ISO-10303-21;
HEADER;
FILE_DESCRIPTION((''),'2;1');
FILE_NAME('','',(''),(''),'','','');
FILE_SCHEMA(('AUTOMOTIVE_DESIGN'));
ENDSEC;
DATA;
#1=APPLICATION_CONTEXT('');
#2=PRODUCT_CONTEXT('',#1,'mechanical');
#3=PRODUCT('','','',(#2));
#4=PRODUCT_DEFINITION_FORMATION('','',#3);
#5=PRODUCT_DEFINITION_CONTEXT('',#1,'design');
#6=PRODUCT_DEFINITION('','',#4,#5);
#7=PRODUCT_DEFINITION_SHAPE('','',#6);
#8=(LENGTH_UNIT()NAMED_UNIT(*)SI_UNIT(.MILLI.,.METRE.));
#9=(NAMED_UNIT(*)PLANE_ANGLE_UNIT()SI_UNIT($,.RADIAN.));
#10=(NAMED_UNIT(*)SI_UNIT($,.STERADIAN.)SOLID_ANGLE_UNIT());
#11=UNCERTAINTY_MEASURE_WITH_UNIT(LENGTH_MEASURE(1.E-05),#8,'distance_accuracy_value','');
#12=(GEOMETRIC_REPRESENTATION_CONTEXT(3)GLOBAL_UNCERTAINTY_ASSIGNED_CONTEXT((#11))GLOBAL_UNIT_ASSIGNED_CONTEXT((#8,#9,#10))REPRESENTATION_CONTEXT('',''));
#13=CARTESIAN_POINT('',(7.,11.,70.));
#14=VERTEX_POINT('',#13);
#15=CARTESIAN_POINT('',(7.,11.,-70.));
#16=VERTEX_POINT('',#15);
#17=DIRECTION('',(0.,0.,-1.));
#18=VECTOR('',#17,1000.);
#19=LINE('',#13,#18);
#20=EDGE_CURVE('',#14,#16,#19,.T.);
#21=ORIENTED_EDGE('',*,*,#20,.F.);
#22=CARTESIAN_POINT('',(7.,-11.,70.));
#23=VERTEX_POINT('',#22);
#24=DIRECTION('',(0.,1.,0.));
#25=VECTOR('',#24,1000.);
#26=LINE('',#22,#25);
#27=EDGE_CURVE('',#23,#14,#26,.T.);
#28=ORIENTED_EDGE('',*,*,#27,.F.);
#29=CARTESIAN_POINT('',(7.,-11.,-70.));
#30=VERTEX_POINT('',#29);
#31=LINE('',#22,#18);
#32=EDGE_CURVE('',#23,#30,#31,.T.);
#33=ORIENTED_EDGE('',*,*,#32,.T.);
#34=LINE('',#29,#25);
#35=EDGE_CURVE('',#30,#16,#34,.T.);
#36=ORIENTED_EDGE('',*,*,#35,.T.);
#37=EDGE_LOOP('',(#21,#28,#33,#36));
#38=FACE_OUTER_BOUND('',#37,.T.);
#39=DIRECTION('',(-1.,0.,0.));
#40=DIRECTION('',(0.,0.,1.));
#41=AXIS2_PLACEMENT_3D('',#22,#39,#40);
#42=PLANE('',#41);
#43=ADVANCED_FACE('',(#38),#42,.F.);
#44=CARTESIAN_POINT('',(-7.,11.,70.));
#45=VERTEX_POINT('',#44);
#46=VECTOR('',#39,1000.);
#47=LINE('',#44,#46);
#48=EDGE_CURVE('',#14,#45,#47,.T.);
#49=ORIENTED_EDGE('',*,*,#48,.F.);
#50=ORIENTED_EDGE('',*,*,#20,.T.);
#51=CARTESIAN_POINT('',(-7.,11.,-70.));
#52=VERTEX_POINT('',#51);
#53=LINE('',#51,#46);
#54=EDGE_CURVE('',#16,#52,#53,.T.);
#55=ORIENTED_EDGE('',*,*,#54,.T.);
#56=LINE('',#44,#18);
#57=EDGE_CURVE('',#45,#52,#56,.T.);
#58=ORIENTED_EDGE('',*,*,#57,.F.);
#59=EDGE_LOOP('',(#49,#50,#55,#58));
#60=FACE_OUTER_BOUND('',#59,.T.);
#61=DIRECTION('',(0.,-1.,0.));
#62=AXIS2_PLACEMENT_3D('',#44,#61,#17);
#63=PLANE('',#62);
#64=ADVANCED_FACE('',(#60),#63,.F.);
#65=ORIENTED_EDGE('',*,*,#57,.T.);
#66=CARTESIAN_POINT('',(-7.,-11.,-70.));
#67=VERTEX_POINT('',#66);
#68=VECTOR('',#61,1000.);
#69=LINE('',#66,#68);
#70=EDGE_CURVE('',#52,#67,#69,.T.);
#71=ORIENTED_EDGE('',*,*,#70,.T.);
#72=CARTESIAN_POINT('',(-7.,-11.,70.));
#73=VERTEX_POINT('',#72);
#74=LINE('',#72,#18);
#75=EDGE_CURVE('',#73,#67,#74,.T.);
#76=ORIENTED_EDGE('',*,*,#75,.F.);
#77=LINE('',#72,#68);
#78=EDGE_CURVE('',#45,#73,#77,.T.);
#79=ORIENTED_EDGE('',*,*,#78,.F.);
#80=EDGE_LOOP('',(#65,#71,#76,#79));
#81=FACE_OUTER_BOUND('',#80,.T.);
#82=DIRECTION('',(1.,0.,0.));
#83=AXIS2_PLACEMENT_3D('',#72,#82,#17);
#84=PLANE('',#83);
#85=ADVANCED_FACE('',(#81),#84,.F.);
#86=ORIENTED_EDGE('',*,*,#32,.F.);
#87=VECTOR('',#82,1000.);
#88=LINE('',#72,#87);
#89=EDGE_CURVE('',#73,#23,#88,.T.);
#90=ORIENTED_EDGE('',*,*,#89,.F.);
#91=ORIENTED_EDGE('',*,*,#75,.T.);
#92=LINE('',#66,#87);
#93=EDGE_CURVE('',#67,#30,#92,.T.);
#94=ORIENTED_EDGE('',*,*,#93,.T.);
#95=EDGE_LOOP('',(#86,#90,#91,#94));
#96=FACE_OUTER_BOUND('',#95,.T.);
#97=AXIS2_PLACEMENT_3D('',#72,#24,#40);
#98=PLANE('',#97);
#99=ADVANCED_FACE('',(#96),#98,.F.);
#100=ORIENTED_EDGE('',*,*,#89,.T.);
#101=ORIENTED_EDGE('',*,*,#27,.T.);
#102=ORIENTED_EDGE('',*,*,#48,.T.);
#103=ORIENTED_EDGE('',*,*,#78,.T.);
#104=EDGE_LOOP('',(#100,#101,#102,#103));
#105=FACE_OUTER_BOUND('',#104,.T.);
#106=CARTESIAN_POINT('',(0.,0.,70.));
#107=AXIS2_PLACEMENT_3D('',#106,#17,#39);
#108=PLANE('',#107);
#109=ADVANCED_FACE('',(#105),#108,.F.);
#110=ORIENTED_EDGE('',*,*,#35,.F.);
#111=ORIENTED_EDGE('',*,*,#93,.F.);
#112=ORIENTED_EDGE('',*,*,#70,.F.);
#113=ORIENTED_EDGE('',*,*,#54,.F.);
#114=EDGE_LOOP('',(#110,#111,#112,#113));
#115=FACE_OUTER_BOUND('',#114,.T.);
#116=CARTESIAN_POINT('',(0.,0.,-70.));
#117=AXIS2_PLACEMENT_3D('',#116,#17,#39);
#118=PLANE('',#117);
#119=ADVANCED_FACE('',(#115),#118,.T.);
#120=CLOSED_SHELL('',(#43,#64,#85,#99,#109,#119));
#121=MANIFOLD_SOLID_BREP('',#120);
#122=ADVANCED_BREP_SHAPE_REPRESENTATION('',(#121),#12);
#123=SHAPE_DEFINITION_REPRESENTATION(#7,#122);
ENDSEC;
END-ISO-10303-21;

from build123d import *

# Parameters (mm, degrees)
KEY_SECTION_22X14_SKETCH_W = 14
KEY_SECTION_22X14_SKETCH_H = 22
KEY_BODY_140MM_DEPTH       = 70


with BuildPart() as part:
    # Key Section 22x14 Sketch → Key Body 140mm (new, symmetric)
    with BuildSketch(Plane.XY):
        Rectangle(KEY_SECTION_22X14_SKETCH_W, KEY_SECTION_22X14_SKETCH_H)
    extrude(amount=KEY_BODY_140MM_DEPTH, both=True)


solid = part.part
